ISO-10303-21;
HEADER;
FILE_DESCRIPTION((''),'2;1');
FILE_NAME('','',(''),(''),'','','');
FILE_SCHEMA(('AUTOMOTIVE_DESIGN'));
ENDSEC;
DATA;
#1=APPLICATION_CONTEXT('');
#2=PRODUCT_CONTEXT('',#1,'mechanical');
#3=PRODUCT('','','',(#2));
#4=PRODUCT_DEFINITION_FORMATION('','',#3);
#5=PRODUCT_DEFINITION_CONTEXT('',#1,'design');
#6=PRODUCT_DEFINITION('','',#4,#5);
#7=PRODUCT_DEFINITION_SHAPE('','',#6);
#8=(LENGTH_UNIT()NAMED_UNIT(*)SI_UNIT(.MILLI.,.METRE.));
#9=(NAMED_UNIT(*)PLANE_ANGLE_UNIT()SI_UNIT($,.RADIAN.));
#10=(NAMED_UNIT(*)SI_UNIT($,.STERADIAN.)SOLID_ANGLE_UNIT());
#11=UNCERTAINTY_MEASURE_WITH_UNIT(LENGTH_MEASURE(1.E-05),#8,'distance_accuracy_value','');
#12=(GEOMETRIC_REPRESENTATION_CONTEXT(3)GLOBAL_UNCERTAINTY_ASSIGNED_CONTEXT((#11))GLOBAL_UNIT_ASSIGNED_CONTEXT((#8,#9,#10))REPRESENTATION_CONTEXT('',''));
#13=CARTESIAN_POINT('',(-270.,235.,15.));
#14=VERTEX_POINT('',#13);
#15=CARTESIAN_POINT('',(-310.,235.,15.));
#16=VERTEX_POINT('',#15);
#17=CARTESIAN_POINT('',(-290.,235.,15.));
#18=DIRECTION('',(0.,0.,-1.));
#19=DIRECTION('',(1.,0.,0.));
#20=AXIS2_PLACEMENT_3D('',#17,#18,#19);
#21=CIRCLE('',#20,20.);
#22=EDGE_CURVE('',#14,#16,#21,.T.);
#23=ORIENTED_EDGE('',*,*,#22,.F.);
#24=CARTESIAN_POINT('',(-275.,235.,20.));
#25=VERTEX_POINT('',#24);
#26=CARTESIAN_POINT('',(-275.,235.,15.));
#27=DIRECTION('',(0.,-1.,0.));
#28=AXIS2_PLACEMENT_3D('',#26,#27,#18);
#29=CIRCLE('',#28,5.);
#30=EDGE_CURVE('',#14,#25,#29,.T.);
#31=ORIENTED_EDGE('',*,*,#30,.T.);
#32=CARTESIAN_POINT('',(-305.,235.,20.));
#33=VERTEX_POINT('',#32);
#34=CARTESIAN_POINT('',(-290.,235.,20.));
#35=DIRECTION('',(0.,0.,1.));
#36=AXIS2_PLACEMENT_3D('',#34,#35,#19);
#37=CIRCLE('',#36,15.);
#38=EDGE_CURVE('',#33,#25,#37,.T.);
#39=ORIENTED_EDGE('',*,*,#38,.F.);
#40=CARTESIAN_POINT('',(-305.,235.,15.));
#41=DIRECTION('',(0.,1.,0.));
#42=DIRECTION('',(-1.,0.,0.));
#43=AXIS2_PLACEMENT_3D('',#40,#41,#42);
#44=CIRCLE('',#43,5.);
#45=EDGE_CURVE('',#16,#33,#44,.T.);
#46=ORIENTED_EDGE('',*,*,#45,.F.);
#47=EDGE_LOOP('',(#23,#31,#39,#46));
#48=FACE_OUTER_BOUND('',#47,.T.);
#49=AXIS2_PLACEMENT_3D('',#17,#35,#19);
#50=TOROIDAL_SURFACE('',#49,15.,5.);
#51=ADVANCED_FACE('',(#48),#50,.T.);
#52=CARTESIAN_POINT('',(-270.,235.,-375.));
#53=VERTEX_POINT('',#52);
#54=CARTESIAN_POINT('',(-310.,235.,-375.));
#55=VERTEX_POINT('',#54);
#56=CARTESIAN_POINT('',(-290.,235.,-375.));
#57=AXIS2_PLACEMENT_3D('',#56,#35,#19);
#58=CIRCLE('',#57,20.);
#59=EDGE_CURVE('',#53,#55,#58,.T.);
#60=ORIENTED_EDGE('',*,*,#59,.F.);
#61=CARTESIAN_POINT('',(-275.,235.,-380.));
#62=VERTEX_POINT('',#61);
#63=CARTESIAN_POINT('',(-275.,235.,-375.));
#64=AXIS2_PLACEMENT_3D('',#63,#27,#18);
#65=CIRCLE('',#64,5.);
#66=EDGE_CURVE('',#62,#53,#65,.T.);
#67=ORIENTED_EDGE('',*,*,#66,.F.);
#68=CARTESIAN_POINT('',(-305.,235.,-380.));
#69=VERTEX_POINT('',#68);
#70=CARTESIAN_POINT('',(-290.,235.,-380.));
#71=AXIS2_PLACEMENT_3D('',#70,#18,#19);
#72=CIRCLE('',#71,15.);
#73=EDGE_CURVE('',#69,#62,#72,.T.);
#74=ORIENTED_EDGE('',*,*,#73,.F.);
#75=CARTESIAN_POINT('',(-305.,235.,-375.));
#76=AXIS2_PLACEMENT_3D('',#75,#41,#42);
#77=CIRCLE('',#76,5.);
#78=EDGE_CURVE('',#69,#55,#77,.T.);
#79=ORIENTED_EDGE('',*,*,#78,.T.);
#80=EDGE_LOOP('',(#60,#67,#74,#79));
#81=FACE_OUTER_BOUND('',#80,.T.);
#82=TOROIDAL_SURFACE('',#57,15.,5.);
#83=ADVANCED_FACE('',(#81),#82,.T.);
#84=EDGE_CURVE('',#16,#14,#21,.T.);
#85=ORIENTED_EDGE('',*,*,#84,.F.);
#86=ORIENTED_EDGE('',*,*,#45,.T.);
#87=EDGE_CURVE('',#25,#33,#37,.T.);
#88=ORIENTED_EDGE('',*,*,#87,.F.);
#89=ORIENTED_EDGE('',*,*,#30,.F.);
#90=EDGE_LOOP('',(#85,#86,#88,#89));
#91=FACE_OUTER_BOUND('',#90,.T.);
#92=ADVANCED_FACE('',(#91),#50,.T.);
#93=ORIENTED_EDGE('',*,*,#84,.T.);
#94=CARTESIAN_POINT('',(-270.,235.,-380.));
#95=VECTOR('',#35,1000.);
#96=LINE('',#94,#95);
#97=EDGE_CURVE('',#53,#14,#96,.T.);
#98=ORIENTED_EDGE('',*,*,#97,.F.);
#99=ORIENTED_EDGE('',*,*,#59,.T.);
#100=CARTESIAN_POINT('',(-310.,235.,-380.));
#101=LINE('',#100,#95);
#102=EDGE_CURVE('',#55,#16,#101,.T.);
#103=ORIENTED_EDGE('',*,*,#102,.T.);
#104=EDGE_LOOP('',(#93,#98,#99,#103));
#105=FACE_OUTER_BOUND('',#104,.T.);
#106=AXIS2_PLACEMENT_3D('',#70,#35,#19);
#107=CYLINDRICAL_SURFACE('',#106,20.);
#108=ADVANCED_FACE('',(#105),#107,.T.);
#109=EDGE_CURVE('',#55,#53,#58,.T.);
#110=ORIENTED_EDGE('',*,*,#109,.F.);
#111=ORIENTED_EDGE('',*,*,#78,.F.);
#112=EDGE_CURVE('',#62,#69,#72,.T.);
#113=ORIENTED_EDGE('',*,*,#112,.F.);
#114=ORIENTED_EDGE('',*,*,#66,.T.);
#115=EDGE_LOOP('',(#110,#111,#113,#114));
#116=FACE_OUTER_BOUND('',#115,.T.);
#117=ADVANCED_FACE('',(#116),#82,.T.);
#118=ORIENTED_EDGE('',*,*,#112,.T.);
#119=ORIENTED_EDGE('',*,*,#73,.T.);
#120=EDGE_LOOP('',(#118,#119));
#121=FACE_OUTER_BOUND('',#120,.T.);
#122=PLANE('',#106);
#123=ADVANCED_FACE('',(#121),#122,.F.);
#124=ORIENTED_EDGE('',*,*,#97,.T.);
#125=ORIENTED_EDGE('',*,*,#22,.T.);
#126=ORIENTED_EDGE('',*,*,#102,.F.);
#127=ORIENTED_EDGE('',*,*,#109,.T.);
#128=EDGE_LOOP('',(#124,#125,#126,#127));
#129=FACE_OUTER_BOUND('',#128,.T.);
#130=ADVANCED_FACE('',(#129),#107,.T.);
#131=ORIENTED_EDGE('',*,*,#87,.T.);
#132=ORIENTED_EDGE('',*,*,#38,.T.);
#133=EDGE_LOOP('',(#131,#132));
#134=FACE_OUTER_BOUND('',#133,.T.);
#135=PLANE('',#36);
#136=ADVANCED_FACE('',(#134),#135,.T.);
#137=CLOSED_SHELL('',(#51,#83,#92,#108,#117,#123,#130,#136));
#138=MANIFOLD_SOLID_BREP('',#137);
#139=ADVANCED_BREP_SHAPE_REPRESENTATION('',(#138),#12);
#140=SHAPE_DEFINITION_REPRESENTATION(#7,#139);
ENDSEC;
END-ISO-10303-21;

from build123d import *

# Parameters (mm, degrees)
BOSS_EXTRUDE1_DEPTH      = 20
BOSS_EXTRUDE1_DEPTH_BACK = 380
SKETCH1_R                = 20
FILLET1_R                = 5


with BuildPart() as part:
    # Sketch1 → Boss-Extrude1 (new, two sides: drawn at the far end of the back side and taken through both)
    with BuildSketch(Plane.XY.offset(-BOSS_EXTRUDE1_DEPTH_BACK)):
        with Locations((-290, 235)):
            Circle(SKETCH1_R)
    extrude(amount=BOSS_EXTRUDE1_DEPTH + BOSS_EXTRUDE1_DEPTH_BACK)

    # Fillet1
    fillet1_edges = [part.edges().sort_by_distance(p)[0] for p in [
        (-310, 235, 20),
        (-310, 235, -380),
    ]]
    fillet(fillet1_edges, radius=FILLET1_R)


solid = part.part
